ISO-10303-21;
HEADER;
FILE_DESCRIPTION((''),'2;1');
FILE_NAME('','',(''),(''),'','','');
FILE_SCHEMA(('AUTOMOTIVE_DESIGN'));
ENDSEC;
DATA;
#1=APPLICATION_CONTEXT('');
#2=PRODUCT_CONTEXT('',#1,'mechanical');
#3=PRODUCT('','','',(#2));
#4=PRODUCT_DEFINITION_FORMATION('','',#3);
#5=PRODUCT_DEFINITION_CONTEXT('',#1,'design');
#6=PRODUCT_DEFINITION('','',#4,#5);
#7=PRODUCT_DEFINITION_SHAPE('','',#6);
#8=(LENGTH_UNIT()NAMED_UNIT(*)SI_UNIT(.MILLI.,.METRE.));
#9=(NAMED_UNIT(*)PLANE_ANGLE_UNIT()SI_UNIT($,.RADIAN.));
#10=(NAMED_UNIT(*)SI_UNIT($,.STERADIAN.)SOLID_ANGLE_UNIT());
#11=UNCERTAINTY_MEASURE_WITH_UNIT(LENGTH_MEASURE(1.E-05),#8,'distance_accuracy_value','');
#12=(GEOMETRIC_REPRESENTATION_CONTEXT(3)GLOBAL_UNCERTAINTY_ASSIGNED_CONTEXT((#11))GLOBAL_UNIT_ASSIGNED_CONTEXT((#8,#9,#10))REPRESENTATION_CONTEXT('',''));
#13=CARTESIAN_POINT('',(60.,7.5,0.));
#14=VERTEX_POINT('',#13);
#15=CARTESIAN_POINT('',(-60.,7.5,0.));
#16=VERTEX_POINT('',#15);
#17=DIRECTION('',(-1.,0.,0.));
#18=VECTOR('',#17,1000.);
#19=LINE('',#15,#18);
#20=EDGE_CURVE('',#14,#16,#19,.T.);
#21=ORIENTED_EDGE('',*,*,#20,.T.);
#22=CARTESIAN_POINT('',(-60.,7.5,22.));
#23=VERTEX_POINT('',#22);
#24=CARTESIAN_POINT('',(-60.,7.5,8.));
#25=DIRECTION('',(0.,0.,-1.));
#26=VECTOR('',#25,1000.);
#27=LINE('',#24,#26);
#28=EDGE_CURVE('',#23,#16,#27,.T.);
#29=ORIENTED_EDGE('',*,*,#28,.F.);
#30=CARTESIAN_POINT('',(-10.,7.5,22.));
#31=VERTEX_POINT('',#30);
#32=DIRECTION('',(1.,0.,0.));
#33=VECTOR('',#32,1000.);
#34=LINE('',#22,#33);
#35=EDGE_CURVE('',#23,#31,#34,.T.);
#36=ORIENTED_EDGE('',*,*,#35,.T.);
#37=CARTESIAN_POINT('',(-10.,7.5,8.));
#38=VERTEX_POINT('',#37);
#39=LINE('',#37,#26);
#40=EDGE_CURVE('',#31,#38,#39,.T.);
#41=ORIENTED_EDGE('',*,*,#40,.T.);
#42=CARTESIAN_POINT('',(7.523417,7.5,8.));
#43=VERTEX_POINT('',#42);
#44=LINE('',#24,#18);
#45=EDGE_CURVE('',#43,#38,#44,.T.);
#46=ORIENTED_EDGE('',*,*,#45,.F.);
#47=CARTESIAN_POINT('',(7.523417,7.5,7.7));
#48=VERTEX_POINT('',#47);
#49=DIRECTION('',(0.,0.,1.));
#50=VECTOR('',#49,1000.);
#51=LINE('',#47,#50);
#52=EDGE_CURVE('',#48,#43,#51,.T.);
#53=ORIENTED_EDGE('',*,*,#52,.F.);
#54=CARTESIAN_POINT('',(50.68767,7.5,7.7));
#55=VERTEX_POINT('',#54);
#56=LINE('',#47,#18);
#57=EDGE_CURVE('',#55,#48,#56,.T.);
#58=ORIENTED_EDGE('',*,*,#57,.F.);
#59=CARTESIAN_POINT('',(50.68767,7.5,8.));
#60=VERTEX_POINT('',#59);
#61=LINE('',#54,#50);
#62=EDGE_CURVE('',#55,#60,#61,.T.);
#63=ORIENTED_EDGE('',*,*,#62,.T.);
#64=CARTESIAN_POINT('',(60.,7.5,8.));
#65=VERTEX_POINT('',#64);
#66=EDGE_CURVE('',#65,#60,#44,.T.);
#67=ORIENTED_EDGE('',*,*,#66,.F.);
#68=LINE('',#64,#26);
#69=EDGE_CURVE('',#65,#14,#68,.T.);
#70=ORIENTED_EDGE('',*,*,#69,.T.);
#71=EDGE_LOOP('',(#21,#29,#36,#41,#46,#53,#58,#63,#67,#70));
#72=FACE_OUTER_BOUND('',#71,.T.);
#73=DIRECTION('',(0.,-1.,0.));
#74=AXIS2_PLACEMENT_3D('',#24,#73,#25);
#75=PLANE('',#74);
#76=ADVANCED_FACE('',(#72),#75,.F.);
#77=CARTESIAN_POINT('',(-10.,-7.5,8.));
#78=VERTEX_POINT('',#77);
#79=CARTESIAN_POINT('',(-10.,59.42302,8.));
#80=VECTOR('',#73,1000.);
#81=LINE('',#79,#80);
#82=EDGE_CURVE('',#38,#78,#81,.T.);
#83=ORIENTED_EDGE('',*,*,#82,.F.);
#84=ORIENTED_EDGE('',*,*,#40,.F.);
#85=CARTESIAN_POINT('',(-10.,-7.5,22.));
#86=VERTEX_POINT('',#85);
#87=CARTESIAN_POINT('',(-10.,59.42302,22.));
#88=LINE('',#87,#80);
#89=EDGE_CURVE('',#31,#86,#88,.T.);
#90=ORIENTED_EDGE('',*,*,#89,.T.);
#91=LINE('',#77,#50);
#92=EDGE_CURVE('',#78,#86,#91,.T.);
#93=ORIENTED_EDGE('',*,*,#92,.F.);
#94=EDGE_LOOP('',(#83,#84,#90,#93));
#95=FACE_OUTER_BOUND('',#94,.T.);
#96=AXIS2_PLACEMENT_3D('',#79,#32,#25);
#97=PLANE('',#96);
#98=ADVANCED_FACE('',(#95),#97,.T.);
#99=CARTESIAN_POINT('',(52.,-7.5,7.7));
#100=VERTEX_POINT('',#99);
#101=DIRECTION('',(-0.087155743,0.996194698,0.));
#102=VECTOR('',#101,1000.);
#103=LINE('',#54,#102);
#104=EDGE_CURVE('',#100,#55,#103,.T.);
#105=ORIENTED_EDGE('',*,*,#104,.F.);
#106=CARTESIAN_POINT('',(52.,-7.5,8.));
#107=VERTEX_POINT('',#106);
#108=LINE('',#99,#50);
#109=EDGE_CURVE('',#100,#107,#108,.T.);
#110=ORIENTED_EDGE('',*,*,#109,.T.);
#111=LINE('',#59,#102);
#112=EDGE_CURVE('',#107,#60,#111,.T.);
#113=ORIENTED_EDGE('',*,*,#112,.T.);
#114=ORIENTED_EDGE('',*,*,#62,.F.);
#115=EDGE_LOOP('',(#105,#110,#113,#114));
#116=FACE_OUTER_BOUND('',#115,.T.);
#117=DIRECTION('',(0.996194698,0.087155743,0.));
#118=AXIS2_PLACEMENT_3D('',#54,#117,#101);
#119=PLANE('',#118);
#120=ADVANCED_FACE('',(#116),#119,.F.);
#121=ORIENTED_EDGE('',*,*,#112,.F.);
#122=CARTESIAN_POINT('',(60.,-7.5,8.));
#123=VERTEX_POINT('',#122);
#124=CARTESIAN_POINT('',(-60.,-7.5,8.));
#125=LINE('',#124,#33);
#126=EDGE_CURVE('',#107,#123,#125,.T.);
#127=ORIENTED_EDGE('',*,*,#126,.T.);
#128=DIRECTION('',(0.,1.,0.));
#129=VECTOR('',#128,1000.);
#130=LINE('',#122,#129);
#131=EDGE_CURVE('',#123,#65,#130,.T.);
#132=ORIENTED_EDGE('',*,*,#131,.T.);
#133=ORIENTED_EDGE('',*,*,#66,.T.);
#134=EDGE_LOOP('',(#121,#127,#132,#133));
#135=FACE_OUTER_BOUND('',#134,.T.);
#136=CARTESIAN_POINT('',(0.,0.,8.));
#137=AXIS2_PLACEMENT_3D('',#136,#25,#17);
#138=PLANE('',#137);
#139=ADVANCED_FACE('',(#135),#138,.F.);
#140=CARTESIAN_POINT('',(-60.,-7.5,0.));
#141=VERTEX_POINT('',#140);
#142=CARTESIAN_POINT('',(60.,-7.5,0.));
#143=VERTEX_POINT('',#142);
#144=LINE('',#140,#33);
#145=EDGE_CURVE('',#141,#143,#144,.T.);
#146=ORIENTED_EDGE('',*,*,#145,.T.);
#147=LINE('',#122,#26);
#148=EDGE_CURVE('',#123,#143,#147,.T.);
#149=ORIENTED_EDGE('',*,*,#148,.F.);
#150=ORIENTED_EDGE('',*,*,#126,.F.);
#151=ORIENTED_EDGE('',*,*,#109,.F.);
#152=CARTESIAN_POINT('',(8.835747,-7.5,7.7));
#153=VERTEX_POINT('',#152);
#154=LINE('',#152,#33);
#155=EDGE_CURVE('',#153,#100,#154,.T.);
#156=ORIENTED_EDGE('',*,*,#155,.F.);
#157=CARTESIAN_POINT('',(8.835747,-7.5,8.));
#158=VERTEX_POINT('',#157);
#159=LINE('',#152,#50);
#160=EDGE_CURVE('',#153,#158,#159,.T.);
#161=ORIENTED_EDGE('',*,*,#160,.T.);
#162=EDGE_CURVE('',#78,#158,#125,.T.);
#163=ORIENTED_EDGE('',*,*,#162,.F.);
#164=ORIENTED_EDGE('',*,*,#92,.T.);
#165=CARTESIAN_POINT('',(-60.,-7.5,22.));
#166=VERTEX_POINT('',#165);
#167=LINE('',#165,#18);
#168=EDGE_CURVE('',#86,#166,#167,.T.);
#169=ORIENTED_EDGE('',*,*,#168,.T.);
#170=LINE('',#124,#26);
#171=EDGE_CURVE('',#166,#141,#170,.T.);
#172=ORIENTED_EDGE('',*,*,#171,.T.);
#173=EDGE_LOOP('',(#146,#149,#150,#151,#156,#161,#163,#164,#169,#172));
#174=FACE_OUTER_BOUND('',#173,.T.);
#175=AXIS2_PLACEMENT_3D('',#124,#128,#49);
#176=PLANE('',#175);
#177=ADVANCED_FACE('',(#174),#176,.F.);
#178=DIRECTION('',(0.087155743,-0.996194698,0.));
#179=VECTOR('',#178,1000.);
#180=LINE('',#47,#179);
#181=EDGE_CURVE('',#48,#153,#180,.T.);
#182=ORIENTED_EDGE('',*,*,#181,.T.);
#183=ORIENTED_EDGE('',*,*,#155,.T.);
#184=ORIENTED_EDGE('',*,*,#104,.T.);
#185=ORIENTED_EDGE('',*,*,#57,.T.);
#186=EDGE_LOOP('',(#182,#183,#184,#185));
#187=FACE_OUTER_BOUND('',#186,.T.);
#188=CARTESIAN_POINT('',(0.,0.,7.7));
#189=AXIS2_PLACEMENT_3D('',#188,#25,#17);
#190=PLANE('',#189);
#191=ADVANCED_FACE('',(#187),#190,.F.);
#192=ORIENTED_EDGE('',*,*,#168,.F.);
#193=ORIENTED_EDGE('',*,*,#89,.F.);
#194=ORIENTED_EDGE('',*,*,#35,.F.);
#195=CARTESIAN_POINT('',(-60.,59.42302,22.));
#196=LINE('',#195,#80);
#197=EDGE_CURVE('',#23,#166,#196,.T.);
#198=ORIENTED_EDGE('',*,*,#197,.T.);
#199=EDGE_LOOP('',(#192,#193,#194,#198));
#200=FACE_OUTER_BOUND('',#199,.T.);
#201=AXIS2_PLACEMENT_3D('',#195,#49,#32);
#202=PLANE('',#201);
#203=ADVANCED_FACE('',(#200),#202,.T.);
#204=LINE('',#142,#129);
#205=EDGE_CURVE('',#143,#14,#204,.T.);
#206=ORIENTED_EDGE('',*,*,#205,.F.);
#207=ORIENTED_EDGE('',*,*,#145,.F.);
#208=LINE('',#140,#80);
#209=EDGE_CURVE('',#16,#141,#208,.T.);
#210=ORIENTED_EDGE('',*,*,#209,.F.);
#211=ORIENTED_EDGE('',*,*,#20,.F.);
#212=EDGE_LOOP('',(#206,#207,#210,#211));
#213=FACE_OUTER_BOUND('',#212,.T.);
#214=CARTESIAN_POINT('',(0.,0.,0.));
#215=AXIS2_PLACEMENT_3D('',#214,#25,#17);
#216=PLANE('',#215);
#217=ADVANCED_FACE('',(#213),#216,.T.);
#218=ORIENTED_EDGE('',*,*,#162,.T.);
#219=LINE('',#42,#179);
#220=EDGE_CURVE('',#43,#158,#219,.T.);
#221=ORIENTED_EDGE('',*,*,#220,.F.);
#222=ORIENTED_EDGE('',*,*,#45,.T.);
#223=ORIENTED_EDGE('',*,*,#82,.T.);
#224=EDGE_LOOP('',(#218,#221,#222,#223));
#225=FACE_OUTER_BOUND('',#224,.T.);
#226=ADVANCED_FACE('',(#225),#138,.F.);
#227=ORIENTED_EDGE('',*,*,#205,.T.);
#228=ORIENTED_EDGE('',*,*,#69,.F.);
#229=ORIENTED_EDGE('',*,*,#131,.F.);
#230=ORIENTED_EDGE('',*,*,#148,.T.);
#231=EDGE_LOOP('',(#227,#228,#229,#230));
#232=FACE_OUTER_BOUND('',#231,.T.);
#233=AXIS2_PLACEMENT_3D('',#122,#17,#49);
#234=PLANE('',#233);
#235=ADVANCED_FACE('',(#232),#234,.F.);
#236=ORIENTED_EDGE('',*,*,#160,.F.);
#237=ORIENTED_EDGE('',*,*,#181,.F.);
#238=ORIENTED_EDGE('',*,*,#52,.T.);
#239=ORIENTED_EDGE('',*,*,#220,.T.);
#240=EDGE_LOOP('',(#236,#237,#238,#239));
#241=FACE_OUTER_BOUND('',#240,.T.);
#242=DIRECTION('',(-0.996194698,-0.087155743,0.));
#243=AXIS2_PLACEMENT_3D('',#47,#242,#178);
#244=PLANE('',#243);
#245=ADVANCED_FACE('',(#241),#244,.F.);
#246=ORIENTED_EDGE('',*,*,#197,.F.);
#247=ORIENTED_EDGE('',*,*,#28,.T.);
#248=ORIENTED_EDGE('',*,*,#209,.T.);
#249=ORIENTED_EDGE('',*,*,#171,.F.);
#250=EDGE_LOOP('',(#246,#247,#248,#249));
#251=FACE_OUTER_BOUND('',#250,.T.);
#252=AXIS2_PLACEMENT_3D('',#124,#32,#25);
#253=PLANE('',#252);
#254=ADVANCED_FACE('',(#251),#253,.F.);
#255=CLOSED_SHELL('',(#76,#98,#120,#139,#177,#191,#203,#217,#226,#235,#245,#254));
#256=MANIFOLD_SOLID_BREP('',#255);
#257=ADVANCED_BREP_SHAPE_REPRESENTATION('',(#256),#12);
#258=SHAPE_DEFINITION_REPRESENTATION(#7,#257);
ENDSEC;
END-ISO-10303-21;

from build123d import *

# Parameters (mm, degrees)
SKETCH_1_W          = 120
SKETCH_1_H          = 15
EXTRUDE_1_DEPTH     = 8
CUT_EXTRUDE_1_DEPTH = 0.3
SKETCH_6_W          = 50
SKETCH_6_H          = 14
EXTRUDE_2_DEPTH     = 15


with BuildPart() as part:
    # 草图1 → 凸台-拉伸1 (new body)
    with BuildSketch(Plane.XY):
        Rectangle(SKETCH_1_W, SKETCH_1_H)
    extrude(amount=EXTRUDE_1_DEPTH)

    # 草图2 → 切除-拉伸1 (cut)
    with BuildSketch(Plane.XY.offset(8)):
        Polygon((50.687670047, 7.5), (52, -7.5), (8.835746986, -7.5), (7.523417033, 7.5), align=None)
    extrude(amount=-CUT_EXTRUDE_1_DEPTH, mode=Mode.SUBTRACT)

    # 草图6 → 凸台-拉伸2 (add)
    with BuildSketch(Plane.XZ.offset(7.5)):
        with Locations((-35, 15)):
            Rectangle(SKETCH_6_W, SKETCH_6_H)
    extrude(amount=-EXTRUDE_2_DEPTH)


solid = part.part
